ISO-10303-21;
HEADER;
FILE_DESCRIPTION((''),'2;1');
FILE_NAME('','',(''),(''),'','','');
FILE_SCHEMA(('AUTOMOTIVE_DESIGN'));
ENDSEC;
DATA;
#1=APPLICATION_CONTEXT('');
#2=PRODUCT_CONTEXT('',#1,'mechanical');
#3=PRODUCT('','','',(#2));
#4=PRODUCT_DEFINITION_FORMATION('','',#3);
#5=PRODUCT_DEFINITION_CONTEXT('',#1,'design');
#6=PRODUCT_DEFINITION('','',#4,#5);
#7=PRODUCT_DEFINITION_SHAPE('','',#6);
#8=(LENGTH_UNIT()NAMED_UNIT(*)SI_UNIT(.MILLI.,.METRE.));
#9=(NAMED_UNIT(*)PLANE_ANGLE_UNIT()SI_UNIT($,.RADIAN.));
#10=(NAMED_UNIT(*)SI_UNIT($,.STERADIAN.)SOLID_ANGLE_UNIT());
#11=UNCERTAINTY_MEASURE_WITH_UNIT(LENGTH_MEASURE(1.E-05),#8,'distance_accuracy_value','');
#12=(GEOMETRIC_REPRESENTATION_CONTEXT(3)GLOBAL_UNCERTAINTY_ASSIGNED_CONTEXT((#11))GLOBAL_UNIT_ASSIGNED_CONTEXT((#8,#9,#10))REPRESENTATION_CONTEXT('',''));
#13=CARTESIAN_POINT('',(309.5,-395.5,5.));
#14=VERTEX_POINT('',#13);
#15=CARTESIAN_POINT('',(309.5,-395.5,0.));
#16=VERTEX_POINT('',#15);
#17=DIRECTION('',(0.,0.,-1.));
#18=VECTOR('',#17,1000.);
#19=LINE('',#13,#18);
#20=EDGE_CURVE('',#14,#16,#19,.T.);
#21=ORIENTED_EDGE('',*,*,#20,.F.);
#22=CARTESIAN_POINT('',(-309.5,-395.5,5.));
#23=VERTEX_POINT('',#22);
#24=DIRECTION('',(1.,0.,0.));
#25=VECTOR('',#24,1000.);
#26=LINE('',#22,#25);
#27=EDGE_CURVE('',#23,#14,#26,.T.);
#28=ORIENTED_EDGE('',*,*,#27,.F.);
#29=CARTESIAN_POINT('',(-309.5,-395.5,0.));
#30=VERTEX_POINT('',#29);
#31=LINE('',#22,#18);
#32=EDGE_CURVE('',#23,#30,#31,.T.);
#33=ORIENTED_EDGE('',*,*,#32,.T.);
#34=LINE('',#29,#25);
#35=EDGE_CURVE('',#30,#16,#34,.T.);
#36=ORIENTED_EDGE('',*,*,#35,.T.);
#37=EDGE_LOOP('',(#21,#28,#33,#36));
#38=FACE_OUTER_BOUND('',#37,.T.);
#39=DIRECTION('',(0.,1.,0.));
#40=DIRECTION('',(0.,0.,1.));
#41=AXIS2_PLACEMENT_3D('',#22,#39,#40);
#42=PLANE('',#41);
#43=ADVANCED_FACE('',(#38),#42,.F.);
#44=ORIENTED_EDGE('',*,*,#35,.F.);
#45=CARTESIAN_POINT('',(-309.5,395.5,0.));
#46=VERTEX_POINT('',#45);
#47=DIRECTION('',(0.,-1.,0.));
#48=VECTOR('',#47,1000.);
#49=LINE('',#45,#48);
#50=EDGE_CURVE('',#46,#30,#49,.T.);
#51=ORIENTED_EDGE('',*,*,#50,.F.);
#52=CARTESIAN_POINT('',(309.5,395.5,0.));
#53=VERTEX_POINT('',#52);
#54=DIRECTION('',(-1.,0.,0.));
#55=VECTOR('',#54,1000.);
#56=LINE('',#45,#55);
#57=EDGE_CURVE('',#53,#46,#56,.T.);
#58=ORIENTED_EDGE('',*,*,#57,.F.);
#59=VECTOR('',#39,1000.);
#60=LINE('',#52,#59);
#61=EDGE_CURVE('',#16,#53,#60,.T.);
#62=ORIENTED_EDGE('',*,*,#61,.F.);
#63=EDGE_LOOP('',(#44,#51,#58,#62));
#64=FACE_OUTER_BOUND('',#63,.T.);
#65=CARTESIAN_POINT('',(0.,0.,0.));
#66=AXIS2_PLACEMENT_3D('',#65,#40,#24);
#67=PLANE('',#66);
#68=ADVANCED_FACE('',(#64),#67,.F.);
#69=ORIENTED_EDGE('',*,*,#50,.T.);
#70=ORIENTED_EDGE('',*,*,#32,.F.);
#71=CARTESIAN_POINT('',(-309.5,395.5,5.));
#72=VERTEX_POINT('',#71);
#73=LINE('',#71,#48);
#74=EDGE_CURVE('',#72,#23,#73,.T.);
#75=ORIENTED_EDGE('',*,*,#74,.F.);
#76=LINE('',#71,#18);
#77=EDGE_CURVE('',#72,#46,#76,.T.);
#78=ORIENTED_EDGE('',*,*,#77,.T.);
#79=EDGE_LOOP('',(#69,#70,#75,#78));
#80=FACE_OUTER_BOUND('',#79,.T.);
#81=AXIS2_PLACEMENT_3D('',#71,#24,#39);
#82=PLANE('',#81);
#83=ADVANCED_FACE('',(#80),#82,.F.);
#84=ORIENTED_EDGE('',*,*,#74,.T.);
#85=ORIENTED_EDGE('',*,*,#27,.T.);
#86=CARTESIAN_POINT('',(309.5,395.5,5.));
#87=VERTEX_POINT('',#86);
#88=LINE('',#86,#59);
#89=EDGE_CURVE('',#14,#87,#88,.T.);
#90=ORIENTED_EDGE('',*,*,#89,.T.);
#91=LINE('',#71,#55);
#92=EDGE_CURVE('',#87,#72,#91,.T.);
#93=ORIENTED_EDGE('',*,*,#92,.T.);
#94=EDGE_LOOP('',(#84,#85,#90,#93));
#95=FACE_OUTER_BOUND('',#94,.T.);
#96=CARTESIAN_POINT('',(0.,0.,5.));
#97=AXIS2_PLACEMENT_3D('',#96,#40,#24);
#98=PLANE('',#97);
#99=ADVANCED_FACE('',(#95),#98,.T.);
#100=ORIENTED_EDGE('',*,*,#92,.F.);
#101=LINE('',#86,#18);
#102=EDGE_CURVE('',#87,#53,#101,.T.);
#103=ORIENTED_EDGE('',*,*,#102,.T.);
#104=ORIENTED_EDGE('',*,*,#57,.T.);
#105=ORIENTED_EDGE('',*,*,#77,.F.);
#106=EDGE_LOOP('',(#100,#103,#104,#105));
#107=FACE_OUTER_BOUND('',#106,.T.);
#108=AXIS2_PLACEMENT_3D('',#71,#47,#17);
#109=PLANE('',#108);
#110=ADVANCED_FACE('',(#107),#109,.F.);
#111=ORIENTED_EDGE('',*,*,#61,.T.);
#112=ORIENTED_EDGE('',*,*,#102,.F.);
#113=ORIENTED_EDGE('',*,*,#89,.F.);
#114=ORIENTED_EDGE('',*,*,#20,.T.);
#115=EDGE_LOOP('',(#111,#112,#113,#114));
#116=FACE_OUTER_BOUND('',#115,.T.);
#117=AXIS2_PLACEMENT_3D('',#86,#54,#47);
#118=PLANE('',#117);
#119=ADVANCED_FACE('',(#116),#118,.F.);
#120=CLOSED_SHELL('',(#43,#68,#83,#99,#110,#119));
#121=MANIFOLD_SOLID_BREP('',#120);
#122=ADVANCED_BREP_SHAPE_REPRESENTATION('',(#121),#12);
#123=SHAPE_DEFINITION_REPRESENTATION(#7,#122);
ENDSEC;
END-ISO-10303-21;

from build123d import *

# Parameters (mm, degrees)
SKETCH_1_W      = 619
SKETCH_1_H      = 791
EXTRUDE_1_DEPTH = 5


with BuildPart() as part:
    # 草图1 → 凸台-拉伸1 (new body)
    with BuildSketch(Plane.XY):
        Rectangle(SKETCH_1_W, SKETCH_1_H)
    extrude(amount=EXTRUDE_1_DEPTH)


solid = part.part
